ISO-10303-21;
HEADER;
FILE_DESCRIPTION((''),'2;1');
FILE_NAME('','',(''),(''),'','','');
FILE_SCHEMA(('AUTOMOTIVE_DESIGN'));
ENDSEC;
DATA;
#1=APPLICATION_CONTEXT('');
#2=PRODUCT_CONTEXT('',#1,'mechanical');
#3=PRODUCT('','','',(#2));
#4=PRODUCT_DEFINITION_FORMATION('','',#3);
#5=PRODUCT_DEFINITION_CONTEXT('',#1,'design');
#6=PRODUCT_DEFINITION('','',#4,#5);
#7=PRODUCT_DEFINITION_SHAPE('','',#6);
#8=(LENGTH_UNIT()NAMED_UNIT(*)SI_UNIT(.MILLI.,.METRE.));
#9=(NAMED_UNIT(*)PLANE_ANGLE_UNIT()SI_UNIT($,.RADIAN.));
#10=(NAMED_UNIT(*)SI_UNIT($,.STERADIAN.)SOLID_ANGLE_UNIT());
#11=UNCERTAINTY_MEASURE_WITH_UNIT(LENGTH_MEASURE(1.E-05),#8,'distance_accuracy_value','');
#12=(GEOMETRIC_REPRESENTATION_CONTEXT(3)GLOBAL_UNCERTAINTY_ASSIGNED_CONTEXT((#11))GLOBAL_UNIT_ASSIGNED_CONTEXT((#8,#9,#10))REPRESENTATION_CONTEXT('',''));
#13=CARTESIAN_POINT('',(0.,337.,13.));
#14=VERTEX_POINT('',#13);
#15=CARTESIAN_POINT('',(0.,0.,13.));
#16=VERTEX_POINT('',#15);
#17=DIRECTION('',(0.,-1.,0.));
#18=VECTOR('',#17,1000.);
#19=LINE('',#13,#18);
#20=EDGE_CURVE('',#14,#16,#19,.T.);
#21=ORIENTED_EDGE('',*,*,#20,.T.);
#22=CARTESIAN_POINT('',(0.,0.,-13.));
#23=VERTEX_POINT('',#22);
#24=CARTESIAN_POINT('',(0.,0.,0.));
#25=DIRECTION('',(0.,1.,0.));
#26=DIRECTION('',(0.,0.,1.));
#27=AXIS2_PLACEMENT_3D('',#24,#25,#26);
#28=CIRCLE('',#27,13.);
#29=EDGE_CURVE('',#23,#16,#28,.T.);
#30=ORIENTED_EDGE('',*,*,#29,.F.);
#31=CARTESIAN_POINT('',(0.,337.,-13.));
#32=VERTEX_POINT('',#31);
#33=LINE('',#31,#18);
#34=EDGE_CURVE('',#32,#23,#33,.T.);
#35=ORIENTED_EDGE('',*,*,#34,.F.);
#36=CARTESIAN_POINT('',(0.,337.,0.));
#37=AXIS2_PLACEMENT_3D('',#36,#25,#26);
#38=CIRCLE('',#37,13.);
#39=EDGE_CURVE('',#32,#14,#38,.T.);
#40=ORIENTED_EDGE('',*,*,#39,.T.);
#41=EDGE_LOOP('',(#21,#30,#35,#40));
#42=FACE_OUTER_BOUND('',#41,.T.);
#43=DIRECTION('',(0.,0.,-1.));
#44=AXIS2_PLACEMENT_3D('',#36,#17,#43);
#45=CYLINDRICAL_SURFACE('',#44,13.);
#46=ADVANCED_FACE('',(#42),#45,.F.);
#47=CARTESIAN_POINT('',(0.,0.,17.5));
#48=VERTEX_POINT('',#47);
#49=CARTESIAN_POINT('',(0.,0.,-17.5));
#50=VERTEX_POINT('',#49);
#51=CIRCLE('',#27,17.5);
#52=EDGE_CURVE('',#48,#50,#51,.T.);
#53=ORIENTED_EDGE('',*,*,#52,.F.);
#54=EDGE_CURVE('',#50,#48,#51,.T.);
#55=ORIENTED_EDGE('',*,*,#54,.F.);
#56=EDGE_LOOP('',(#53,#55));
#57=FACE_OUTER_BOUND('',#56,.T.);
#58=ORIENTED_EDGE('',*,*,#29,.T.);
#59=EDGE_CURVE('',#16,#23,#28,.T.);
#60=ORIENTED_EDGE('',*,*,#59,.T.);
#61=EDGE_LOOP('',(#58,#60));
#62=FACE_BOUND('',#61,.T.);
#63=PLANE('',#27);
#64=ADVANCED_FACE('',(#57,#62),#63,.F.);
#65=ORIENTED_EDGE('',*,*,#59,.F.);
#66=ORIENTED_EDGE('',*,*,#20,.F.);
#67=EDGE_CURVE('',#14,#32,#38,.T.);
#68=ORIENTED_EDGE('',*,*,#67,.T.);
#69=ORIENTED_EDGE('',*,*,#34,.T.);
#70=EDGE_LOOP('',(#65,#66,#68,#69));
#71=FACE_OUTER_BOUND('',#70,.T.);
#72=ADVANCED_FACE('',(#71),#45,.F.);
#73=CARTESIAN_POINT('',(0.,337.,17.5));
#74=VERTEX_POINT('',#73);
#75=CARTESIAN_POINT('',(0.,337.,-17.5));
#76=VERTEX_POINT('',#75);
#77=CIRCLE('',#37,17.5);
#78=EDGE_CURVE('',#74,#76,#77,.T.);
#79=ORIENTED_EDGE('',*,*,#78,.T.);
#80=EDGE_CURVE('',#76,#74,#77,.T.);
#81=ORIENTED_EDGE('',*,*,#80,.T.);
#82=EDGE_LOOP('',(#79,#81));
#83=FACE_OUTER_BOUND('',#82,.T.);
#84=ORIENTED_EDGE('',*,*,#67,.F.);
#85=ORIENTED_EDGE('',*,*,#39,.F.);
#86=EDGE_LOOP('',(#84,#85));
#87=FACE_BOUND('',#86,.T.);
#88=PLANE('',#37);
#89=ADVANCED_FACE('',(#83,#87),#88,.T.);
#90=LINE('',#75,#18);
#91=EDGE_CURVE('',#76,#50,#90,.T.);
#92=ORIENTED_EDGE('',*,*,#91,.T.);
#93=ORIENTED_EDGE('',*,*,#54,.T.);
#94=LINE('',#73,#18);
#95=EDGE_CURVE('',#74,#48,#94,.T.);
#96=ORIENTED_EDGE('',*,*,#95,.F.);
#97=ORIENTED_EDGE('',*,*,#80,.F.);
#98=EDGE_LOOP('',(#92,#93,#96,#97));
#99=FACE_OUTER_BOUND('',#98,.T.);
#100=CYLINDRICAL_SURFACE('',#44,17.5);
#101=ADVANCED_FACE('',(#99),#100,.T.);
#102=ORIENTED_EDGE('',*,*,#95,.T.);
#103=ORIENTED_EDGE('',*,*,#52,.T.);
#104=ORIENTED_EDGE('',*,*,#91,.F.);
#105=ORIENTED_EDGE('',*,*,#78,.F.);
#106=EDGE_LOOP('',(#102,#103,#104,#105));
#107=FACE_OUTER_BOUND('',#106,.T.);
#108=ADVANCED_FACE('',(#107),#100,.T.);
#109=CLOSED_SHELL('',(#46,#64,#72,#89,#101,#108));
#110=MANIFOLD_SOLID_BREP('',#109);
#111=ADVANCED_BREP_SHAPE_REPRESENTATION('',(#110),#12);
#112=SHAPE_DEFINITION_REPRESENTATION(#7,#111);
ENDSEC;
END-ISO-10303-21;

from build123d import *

# Parameters (mm, degrees)
SKETCH_1_R      = 17.5
EXTRUDE_1_DEPTH = 337
SHELL_1_T       = -4.5


with BuildPart() as part:
    # 草图1 → 凸台-拉伸1 (new body)
    with BuildSketch(Plane(origin=(0, 0, 0), x_dir=(1, 0, 0), z_dir=(0, 1, 0))):
        with Locations(Location((0, 0, 0), (0, 0, 270))):
            Circle(SKETCH_1_R)
    extrude(amount=EXTRUDE_1_DEPTH)

    # 抽壳1
    shell_1_openings = [part.faces().sort_by_distance(p)[0] for p in [
        (0, 337, 0),
        (0, 0, 0),
    ]]
    offset(amount=SHELL_1_T, openings=shell_1_openings, kind=Kind.INTERSECTION)


solid = part.part
